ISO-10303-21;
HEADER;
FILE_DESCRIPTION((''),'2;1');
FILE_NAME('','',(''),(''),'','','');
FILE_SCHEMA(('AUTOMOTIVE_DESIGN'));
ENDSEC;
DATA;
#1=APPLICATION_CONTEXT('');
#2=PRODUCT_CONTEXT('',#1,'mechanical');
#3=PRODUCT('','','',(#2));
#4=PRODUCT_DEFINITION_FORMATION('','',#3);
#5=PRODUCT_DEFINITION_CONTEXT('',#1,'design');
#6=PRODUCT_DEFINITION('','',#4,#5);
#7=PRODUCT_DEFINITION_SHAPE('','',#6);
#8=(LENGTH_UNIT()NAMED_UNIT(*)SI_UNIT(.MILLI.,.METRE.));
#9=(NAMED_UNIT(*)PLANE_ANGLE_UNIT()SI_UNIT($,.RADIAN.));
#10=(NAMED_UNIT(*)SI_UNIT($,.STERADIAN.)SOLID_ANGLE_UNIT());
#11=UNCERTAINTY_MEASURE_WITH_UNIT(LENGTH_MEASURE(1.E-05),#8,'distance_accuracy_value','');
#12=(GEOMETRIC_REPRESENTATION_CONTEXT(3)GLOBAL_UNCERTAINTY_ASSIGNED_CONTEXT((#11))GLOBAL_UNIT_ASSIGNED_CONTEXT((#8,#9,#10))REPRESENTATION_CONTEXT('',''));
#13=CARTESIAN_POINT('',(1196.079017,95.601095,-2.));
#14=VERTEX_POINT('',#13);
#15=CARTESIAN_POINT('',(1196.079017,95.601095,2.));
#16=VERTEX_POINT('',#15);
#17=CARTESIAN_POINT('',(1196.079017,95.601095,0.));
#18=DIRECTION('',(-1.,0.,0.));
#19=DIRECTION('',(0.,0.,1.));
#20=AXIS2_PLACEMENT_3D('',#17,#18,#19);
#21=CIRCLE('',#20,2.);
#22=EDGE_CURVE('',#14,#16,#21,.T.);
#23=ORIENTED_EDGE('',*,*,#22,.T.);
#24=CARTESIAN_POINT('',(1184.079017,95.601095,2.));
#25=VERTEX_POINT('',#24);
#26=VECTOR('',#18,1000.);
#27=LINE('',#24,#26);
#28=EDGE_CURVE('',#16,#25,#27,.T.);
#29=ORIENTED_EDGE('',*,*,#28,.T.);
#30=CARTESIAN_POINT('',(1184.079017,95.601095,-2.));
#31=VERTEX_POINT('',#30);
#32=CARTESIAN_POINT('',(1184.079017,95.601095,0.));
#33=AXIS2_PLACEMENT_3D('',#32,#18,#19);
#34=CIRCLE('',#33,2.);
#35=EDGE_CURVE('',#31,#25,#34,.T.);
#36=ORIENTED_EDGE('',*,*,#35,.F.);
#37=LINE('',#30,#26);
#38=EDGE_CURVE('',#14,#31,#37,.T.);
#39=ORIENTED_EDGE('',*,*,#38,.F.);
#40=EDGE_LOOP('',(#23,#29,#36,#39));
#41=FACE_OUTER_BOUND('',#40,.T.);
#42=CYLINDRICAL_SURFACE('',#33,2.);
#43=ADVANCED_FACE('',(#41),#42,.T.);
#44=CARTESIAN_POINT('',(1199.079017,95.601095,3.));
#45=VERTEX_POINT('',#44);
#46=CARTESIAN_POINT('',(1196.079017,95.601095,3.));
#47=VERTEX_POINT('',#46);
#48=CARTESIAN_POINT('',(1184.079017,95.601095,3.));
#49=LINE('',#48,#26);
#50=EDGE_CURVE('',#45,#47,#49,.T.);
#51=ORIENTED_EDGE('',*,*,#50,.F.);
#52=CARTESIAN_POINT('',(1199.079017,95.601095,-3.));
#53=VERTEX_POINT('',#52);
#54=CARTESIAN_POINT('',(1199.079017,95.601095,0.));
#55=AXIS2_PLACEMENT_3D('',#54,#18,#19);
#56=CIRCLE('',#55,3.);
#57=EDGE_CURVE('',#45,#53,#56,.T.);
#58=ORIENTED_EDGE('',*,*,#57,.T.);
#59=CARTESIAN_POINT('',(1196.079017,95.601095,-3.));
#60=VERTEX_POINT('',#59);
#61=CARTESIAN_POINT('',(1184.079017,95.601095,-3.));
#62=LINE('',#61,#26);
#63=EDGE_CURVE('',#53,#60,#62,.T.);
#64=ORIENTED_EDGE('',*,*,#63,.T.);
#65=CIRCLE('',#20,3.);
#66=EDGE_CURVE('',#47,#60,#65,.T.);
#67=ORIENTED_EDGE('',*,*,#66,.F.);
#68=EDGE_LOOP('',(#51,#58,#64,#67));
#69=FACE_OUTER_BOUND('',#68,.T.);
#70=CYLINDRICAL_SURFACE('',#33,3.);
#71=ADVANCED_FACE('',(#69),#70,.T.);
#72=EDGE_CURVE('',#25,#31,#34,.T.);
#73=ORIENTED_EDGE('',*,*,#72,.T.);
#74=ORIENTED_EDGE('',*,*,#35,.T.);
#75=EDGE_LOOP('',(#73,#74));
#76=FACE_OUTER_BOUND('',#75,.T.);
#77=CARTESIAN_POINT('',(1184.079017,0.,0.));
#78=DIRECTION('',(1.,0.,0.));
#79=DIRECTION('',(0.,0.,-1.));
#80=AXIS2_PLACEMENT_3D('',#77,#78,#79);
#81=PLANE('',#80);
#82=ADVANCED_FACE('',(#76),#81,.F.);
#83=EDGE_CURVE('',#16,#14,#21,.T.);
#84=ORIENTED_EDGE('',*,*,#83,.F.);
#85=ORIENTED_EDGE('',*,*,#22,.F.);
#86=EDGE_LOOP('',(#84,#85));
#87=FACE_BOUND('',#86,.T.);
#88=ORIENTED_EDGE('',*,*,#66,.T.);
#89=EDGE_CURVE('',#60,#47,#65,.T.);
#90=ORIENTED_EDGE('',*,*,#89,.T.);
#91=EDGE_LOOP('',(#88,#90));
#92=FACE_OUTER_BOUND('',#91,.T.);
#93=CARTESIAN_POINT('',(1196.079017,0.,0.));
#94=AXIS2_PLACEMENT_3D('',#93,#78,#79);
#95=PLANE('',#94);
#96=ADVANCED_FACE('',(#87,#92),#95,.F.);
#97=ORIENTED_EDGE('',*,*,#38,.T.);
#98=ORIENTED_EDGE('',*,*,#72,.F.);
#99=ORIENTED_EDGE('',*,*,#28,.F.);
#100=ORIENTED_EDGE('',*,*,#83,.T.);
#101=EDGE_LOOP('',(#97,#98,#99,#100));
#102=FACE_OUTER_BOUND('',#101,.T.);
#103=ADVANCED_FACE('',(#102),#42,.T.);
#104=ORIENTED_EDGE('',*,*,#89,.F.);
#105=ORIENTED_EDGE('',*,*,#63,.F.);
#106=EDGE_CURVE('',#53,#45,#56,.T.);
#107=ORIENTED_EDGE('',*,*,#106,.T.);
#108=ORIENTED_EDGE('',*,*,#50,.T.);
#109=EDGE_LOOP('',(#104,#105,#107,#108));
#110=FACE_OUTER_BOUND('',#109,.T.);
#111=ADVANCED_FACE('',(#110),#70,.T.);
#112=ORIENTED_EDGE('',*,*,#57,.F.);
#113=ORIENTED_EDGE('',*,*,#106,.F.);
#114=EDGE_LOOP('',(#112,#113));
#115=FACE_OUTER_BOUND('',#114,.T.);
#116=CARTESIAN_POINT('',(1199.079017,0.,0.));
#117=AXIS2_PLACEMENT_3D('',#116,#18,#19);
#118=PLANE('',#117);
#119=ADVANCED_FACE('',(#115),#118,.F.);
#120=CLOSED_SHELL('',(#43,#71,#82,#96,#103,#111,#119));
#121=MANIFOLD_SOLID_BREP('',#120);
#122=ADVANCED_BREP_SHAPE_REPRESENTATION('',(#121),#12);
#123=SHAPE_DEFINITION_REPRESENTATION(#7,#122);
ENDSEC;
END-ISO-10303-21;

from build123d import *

# Parameters (mm, degrees)
SKETCH1_W = 12
SKETCH1_H = 2


with BuildPart() as part:
    # Sketch1 → Revolve1 (revolve)
    with BuildSketch(Plane.XY, mode=Mode.PRIVATE) as revolve1_sk:
        with Locations((1190.079016837, 96.601095303)):
            Rectangle(SKETCH1_W, SKETCH1_H)
        Polygon((1196.079016837, 98.601095303), (1196.079016837, 97.601095303), (1196.079016837, 95.601095303), (1199.079016837, 95.601095303), (1199.079016837, 98.601095303), align=None)
    revolve(revolve1_sk.sketch.rotate(Axis((1184.079016837, 95.601095303, 0), (1, 0, 0)), 90), axis=Axis((1184.079016837, 95.601095303, 0), (1, 0, 0)))


solid = part.part
